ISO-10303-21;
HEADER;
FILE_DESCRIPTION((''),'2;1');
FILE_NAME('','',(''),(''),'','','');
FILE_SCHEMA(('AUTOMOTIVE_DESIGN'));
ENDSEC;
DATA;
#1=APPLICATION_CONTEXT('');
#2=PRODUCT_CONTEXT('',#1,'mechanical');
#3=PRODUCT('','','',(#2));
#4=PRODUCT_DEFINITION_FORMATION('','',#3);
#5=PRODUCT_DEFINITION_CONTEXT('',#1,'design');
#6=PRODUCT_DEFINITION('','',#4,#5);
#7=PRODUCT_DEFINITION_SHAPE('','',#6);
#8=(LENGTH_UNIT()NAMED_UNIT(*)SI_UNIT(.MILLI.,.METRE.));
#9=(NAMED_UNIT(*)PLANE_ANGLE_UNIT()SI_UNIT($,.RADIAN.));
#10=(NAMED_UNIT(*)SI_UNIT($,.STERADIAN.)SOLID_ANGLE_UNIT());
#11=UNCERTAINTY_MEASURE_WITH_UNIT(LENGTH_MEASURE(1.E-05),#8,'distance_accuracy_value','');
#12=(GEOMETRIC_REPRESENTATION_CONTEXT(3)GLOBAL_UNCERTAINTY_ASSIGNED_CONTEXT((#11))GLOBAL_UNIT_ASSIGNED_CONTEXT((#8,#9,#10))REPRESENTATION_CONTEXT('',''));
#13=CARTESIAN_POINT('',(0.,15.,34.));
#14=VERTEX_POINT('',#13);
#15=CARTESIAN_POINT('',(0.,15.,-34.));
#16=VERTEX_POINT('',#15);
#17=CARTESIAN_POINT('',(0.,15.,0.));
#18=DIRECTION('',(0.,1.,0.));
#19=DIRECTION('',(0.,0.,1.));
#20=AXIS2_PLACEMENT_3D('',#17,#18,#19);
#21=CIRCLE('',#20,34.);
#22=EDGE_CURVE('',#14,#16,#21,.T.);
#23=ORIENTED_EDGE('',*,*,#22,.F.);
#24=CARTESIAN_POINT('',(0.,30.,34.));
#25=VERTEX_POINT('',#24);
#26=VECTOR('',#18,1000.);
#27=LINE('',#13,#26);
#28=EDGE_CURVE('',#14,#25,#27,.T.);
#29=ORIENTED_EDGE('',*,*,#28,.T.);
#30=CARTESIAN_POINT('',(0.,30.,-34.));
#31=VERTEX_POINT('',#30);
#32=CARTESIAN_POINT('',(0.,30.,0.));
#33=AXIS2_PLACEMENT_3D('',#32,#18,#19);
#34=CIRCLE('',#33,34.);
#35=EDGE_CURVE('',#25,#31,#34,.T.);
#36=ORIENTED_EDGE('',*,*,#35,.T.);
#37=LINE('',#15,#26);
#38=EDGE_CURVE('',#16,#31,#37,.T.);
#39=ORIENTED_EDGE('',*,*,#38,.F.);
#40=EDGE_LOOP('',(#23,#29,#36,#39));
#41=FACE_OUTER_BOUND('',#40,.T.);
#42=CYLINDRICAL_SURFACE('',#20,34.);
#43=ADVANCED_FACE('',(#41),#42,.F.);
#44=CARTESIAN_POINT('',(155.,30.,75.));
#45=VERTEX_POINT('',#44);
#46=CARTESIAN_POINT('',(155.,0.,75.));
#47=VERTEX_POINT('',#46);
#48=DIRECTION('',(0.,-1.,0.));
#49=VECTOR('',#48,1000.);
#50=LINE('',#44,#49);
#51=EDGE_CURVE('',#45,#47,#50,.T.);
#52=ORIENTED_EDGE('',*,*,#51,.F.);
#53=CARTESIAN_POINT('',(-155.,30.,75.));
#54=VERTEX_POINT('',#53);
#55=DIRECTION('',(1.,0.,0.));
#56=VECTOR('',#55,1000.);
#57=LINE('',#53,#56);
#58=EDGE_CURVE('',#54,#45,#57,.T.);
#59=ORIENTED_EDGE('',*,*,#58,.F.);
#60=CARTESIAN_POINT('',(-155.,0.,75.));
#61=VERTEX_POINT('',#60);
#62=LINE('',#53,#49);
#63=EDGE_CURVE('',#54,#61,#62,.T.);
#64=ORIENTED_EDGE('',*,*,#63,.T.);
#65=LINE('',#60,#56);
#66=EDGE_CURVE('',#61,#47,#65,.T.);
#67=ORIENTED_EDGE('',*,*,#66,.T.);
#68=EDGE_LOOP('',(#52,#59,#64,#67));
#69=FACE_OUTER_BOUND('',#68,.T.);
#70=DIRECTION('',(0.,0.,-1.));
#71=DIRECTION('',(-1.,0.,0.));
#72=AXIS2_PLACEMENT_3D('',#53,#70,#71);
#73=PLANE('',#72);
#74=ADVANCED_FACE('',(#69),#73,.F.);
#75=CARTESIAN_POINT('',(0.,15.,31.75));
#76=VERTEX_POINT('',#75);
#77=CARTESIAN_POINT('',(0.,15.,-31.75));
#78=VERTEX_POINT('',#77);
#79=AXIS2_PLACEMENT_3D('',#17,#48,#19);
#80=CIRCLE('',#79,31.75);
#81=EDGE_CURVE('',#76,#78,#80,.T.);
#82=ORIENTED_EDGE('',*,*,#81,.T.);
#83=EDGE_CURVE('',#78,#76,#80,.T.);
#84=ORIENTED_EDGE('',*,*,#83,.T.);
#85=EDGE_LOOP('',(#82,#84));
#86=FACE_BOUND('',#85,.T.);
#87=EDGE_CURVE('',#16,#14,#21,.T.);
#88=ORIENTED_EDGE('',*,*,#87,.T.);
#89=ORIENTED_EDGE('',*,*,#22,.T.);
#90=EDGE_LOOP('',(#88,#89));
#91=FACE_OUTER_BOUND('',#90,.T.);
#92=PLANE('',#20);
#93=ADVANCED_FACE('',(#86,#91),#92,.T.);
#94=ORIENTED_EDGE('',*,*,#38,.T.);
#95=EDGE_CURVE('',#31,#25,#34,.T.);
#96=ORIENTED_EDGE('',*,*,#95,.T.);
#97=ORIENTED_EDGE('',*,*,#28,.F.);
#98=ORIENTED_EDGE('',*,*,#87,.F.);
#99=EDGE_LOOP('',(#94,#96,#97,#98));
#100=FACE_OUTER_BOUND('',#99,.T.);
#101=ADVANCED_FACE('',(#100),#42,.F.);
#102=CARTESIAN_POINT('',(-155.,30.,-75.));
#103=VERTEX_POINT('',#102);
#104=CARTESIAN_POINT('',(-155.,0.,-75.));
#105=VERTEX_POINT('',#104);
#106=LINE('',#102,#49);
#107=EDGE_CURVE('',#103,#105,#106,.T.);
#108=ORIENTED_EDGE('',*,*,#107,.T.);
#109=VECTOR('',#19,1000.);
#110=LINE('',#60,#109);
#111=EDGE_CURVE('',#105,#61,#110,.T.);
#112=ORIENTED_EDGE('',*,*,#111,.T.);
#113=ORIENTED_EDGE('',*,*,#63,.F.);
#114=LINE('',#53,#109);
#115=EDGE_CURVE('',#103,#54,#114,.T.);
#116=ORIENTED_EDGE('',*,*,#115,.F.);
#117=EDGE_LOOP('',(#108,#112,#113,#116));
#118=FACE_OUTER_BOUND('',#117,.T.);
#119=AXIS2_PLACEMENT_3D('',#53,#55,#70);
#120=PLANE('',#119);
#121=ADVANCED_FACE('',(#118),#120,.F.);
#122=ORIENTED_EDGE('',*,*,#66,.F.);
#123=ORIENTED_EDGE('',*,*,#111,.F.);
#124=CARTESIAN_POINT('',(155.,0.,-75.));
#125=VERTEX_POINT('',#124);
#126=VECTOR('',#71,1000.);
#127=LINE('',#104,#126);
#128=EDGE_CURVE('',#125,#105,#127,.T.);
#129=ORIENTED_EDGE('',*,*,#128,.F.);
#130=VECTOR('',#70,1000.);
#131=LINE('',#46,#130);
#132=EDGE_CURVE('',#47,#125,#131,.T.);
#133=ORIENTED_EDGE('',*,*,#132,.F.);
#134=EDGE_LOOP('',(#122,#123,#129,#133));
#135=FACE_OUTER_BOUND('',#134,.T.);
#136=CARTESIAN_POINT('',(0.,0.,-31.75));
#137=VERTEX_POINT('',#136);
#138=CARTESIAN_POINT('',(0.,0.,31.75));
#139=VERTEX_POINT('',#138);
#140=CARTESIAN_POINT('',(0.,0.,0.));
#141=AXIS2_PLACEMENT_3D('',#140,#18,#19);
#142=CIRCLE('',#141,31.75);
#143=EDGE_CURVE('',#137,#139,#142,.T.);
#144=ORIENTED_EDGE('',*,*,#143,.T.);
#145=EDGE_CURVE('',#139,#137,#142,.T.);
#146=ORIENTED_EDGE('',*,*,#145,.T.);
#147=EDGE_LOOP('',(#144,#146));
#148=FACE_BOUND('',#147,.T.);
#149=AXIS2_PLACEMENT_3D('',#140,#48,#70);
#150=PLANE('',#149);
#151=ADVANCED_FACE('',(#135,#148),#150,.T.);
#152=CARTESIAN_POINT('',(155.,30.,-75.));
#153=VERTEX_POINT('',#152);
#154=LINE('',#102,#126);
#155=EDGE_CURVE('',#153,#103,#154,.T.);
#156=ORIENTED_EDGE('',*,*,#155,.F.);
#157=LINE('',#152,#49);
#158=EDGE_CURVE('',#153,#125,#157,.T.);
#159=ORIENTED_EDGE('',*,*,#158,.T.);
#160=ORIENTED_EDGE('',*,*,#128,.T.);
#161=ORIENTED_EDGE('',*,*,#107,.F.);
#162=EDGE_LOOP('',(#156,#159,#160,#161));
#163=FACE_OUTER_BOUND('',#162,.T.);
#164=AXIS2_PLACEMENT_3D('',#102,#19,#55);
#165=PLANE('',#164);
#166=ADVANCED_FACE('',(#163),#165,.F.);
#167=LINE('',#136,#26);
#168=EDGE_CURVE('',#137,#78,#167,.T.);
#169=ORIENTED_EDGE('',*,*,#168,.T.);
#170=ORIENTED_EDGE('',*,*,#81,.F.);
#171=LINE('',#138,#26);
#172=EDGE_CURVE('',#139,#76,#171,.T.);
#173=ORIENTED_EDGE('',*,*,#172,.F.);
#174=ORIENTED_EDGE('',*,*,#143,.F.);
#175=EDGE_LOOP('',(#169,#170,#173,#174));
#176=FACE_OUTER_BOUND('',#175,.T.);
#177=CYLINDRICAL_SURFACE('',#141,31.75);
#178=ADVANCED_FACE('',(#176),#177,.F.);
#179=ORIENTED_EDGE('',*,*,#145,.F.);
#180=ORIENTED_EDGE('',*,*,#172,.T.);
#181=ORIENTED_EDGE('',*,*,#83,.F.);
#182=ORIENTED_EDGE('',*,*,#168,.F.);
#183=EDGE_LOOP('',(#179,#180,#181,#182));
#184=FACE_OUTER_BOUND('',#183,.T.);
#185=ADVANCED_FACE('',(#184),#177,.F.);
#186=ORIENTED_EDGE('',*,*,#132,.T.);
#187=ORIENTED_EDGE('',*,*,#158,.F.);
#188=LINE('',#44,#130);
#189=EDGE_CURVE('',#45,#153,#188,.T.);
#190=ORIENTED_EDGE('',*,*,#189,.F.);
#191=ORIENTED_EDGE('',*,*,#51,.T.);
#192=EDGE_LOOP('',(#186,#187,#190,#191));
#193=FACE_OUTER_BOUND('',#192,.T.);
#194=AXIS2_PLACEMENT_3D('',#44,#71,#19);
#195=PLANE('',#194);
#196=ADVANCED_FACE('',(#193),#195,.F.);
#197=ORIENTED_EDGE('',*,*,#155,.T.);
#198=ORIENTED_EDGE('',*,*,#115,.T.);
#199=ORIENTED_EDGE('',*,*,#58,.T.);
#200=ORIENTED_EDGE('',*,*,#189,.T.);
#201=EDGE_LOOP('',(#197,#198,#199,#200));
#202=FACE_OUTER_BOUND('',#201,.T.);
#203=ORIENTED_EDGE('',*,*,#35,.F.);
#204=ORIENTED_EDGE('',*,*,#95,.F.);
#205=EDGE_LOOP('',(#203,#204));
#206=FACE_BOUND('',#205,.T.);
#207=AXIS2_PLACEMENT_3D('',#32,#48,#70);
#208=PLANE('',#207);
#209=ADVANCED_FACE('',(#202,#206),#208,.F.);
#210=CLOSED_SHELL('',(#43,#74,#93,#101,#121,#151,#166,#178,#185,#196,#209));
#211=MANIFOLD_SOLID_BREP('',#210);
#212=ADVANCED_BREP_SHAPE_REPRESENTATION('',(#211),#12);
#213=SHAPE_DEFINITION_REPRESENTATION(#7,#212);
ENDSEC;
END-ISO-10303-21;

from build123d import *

# Parameters (mm, degrees)
SKETCH_1_W          = 310
SKETCH_1_H          = 150
EXTRUDE_1_DEPTH     = 30
SKETCH_2_R          = 31.75
CUT_EXTRUDE_1_DEPTH = 175.785582929
SKETCH_3_R          = 34
CUT_EXTRUDE_2_DEPTH = 15


with BuildPart() as part:
    # 草图1 → 凸台-拉伸1 (new body)
    with BuildSketch(Plane(origin=(0, 0, 0), x_dir=(1, 0, 0), z_dir=(0, 1, 0))):
        Rectangle(SKETCH_1_W, SKETCH_1_H)
    extrude(amount=EXTRUDE_1_DEPTH)

    # 草图2 → 切除-拉伸1 (cut, through all)
    with BuildSketch(Plane(origin=(0, 30, 0), x_dir=(1, 0, 0), z_dir=(0, 1, 0))):
        with Locations(Location((0, 0, 0), (0, 0, 270))):
            Circle(SKETCH_2_R)
    extrude(amount=-CUT_EXTRUDE_1_DEPTH, mode=Mode.SUBTRACT)

    # 草图3 → 切除-拉伸2 (cut)
    with BuildSketch(Plane(origin=(0, 30, 0), x_dir=(1, 0, 0), z_dir=(0, 1, 0))):
        with Locations(Location((0, 0, 0), (0, 0, 270))):
            Circle(SKETCH_3_R)
    extrude(amount=-CUT_EXTRUDE_2_DEPTH, mode=Mode.SUBTRACT)


solid = part.part
